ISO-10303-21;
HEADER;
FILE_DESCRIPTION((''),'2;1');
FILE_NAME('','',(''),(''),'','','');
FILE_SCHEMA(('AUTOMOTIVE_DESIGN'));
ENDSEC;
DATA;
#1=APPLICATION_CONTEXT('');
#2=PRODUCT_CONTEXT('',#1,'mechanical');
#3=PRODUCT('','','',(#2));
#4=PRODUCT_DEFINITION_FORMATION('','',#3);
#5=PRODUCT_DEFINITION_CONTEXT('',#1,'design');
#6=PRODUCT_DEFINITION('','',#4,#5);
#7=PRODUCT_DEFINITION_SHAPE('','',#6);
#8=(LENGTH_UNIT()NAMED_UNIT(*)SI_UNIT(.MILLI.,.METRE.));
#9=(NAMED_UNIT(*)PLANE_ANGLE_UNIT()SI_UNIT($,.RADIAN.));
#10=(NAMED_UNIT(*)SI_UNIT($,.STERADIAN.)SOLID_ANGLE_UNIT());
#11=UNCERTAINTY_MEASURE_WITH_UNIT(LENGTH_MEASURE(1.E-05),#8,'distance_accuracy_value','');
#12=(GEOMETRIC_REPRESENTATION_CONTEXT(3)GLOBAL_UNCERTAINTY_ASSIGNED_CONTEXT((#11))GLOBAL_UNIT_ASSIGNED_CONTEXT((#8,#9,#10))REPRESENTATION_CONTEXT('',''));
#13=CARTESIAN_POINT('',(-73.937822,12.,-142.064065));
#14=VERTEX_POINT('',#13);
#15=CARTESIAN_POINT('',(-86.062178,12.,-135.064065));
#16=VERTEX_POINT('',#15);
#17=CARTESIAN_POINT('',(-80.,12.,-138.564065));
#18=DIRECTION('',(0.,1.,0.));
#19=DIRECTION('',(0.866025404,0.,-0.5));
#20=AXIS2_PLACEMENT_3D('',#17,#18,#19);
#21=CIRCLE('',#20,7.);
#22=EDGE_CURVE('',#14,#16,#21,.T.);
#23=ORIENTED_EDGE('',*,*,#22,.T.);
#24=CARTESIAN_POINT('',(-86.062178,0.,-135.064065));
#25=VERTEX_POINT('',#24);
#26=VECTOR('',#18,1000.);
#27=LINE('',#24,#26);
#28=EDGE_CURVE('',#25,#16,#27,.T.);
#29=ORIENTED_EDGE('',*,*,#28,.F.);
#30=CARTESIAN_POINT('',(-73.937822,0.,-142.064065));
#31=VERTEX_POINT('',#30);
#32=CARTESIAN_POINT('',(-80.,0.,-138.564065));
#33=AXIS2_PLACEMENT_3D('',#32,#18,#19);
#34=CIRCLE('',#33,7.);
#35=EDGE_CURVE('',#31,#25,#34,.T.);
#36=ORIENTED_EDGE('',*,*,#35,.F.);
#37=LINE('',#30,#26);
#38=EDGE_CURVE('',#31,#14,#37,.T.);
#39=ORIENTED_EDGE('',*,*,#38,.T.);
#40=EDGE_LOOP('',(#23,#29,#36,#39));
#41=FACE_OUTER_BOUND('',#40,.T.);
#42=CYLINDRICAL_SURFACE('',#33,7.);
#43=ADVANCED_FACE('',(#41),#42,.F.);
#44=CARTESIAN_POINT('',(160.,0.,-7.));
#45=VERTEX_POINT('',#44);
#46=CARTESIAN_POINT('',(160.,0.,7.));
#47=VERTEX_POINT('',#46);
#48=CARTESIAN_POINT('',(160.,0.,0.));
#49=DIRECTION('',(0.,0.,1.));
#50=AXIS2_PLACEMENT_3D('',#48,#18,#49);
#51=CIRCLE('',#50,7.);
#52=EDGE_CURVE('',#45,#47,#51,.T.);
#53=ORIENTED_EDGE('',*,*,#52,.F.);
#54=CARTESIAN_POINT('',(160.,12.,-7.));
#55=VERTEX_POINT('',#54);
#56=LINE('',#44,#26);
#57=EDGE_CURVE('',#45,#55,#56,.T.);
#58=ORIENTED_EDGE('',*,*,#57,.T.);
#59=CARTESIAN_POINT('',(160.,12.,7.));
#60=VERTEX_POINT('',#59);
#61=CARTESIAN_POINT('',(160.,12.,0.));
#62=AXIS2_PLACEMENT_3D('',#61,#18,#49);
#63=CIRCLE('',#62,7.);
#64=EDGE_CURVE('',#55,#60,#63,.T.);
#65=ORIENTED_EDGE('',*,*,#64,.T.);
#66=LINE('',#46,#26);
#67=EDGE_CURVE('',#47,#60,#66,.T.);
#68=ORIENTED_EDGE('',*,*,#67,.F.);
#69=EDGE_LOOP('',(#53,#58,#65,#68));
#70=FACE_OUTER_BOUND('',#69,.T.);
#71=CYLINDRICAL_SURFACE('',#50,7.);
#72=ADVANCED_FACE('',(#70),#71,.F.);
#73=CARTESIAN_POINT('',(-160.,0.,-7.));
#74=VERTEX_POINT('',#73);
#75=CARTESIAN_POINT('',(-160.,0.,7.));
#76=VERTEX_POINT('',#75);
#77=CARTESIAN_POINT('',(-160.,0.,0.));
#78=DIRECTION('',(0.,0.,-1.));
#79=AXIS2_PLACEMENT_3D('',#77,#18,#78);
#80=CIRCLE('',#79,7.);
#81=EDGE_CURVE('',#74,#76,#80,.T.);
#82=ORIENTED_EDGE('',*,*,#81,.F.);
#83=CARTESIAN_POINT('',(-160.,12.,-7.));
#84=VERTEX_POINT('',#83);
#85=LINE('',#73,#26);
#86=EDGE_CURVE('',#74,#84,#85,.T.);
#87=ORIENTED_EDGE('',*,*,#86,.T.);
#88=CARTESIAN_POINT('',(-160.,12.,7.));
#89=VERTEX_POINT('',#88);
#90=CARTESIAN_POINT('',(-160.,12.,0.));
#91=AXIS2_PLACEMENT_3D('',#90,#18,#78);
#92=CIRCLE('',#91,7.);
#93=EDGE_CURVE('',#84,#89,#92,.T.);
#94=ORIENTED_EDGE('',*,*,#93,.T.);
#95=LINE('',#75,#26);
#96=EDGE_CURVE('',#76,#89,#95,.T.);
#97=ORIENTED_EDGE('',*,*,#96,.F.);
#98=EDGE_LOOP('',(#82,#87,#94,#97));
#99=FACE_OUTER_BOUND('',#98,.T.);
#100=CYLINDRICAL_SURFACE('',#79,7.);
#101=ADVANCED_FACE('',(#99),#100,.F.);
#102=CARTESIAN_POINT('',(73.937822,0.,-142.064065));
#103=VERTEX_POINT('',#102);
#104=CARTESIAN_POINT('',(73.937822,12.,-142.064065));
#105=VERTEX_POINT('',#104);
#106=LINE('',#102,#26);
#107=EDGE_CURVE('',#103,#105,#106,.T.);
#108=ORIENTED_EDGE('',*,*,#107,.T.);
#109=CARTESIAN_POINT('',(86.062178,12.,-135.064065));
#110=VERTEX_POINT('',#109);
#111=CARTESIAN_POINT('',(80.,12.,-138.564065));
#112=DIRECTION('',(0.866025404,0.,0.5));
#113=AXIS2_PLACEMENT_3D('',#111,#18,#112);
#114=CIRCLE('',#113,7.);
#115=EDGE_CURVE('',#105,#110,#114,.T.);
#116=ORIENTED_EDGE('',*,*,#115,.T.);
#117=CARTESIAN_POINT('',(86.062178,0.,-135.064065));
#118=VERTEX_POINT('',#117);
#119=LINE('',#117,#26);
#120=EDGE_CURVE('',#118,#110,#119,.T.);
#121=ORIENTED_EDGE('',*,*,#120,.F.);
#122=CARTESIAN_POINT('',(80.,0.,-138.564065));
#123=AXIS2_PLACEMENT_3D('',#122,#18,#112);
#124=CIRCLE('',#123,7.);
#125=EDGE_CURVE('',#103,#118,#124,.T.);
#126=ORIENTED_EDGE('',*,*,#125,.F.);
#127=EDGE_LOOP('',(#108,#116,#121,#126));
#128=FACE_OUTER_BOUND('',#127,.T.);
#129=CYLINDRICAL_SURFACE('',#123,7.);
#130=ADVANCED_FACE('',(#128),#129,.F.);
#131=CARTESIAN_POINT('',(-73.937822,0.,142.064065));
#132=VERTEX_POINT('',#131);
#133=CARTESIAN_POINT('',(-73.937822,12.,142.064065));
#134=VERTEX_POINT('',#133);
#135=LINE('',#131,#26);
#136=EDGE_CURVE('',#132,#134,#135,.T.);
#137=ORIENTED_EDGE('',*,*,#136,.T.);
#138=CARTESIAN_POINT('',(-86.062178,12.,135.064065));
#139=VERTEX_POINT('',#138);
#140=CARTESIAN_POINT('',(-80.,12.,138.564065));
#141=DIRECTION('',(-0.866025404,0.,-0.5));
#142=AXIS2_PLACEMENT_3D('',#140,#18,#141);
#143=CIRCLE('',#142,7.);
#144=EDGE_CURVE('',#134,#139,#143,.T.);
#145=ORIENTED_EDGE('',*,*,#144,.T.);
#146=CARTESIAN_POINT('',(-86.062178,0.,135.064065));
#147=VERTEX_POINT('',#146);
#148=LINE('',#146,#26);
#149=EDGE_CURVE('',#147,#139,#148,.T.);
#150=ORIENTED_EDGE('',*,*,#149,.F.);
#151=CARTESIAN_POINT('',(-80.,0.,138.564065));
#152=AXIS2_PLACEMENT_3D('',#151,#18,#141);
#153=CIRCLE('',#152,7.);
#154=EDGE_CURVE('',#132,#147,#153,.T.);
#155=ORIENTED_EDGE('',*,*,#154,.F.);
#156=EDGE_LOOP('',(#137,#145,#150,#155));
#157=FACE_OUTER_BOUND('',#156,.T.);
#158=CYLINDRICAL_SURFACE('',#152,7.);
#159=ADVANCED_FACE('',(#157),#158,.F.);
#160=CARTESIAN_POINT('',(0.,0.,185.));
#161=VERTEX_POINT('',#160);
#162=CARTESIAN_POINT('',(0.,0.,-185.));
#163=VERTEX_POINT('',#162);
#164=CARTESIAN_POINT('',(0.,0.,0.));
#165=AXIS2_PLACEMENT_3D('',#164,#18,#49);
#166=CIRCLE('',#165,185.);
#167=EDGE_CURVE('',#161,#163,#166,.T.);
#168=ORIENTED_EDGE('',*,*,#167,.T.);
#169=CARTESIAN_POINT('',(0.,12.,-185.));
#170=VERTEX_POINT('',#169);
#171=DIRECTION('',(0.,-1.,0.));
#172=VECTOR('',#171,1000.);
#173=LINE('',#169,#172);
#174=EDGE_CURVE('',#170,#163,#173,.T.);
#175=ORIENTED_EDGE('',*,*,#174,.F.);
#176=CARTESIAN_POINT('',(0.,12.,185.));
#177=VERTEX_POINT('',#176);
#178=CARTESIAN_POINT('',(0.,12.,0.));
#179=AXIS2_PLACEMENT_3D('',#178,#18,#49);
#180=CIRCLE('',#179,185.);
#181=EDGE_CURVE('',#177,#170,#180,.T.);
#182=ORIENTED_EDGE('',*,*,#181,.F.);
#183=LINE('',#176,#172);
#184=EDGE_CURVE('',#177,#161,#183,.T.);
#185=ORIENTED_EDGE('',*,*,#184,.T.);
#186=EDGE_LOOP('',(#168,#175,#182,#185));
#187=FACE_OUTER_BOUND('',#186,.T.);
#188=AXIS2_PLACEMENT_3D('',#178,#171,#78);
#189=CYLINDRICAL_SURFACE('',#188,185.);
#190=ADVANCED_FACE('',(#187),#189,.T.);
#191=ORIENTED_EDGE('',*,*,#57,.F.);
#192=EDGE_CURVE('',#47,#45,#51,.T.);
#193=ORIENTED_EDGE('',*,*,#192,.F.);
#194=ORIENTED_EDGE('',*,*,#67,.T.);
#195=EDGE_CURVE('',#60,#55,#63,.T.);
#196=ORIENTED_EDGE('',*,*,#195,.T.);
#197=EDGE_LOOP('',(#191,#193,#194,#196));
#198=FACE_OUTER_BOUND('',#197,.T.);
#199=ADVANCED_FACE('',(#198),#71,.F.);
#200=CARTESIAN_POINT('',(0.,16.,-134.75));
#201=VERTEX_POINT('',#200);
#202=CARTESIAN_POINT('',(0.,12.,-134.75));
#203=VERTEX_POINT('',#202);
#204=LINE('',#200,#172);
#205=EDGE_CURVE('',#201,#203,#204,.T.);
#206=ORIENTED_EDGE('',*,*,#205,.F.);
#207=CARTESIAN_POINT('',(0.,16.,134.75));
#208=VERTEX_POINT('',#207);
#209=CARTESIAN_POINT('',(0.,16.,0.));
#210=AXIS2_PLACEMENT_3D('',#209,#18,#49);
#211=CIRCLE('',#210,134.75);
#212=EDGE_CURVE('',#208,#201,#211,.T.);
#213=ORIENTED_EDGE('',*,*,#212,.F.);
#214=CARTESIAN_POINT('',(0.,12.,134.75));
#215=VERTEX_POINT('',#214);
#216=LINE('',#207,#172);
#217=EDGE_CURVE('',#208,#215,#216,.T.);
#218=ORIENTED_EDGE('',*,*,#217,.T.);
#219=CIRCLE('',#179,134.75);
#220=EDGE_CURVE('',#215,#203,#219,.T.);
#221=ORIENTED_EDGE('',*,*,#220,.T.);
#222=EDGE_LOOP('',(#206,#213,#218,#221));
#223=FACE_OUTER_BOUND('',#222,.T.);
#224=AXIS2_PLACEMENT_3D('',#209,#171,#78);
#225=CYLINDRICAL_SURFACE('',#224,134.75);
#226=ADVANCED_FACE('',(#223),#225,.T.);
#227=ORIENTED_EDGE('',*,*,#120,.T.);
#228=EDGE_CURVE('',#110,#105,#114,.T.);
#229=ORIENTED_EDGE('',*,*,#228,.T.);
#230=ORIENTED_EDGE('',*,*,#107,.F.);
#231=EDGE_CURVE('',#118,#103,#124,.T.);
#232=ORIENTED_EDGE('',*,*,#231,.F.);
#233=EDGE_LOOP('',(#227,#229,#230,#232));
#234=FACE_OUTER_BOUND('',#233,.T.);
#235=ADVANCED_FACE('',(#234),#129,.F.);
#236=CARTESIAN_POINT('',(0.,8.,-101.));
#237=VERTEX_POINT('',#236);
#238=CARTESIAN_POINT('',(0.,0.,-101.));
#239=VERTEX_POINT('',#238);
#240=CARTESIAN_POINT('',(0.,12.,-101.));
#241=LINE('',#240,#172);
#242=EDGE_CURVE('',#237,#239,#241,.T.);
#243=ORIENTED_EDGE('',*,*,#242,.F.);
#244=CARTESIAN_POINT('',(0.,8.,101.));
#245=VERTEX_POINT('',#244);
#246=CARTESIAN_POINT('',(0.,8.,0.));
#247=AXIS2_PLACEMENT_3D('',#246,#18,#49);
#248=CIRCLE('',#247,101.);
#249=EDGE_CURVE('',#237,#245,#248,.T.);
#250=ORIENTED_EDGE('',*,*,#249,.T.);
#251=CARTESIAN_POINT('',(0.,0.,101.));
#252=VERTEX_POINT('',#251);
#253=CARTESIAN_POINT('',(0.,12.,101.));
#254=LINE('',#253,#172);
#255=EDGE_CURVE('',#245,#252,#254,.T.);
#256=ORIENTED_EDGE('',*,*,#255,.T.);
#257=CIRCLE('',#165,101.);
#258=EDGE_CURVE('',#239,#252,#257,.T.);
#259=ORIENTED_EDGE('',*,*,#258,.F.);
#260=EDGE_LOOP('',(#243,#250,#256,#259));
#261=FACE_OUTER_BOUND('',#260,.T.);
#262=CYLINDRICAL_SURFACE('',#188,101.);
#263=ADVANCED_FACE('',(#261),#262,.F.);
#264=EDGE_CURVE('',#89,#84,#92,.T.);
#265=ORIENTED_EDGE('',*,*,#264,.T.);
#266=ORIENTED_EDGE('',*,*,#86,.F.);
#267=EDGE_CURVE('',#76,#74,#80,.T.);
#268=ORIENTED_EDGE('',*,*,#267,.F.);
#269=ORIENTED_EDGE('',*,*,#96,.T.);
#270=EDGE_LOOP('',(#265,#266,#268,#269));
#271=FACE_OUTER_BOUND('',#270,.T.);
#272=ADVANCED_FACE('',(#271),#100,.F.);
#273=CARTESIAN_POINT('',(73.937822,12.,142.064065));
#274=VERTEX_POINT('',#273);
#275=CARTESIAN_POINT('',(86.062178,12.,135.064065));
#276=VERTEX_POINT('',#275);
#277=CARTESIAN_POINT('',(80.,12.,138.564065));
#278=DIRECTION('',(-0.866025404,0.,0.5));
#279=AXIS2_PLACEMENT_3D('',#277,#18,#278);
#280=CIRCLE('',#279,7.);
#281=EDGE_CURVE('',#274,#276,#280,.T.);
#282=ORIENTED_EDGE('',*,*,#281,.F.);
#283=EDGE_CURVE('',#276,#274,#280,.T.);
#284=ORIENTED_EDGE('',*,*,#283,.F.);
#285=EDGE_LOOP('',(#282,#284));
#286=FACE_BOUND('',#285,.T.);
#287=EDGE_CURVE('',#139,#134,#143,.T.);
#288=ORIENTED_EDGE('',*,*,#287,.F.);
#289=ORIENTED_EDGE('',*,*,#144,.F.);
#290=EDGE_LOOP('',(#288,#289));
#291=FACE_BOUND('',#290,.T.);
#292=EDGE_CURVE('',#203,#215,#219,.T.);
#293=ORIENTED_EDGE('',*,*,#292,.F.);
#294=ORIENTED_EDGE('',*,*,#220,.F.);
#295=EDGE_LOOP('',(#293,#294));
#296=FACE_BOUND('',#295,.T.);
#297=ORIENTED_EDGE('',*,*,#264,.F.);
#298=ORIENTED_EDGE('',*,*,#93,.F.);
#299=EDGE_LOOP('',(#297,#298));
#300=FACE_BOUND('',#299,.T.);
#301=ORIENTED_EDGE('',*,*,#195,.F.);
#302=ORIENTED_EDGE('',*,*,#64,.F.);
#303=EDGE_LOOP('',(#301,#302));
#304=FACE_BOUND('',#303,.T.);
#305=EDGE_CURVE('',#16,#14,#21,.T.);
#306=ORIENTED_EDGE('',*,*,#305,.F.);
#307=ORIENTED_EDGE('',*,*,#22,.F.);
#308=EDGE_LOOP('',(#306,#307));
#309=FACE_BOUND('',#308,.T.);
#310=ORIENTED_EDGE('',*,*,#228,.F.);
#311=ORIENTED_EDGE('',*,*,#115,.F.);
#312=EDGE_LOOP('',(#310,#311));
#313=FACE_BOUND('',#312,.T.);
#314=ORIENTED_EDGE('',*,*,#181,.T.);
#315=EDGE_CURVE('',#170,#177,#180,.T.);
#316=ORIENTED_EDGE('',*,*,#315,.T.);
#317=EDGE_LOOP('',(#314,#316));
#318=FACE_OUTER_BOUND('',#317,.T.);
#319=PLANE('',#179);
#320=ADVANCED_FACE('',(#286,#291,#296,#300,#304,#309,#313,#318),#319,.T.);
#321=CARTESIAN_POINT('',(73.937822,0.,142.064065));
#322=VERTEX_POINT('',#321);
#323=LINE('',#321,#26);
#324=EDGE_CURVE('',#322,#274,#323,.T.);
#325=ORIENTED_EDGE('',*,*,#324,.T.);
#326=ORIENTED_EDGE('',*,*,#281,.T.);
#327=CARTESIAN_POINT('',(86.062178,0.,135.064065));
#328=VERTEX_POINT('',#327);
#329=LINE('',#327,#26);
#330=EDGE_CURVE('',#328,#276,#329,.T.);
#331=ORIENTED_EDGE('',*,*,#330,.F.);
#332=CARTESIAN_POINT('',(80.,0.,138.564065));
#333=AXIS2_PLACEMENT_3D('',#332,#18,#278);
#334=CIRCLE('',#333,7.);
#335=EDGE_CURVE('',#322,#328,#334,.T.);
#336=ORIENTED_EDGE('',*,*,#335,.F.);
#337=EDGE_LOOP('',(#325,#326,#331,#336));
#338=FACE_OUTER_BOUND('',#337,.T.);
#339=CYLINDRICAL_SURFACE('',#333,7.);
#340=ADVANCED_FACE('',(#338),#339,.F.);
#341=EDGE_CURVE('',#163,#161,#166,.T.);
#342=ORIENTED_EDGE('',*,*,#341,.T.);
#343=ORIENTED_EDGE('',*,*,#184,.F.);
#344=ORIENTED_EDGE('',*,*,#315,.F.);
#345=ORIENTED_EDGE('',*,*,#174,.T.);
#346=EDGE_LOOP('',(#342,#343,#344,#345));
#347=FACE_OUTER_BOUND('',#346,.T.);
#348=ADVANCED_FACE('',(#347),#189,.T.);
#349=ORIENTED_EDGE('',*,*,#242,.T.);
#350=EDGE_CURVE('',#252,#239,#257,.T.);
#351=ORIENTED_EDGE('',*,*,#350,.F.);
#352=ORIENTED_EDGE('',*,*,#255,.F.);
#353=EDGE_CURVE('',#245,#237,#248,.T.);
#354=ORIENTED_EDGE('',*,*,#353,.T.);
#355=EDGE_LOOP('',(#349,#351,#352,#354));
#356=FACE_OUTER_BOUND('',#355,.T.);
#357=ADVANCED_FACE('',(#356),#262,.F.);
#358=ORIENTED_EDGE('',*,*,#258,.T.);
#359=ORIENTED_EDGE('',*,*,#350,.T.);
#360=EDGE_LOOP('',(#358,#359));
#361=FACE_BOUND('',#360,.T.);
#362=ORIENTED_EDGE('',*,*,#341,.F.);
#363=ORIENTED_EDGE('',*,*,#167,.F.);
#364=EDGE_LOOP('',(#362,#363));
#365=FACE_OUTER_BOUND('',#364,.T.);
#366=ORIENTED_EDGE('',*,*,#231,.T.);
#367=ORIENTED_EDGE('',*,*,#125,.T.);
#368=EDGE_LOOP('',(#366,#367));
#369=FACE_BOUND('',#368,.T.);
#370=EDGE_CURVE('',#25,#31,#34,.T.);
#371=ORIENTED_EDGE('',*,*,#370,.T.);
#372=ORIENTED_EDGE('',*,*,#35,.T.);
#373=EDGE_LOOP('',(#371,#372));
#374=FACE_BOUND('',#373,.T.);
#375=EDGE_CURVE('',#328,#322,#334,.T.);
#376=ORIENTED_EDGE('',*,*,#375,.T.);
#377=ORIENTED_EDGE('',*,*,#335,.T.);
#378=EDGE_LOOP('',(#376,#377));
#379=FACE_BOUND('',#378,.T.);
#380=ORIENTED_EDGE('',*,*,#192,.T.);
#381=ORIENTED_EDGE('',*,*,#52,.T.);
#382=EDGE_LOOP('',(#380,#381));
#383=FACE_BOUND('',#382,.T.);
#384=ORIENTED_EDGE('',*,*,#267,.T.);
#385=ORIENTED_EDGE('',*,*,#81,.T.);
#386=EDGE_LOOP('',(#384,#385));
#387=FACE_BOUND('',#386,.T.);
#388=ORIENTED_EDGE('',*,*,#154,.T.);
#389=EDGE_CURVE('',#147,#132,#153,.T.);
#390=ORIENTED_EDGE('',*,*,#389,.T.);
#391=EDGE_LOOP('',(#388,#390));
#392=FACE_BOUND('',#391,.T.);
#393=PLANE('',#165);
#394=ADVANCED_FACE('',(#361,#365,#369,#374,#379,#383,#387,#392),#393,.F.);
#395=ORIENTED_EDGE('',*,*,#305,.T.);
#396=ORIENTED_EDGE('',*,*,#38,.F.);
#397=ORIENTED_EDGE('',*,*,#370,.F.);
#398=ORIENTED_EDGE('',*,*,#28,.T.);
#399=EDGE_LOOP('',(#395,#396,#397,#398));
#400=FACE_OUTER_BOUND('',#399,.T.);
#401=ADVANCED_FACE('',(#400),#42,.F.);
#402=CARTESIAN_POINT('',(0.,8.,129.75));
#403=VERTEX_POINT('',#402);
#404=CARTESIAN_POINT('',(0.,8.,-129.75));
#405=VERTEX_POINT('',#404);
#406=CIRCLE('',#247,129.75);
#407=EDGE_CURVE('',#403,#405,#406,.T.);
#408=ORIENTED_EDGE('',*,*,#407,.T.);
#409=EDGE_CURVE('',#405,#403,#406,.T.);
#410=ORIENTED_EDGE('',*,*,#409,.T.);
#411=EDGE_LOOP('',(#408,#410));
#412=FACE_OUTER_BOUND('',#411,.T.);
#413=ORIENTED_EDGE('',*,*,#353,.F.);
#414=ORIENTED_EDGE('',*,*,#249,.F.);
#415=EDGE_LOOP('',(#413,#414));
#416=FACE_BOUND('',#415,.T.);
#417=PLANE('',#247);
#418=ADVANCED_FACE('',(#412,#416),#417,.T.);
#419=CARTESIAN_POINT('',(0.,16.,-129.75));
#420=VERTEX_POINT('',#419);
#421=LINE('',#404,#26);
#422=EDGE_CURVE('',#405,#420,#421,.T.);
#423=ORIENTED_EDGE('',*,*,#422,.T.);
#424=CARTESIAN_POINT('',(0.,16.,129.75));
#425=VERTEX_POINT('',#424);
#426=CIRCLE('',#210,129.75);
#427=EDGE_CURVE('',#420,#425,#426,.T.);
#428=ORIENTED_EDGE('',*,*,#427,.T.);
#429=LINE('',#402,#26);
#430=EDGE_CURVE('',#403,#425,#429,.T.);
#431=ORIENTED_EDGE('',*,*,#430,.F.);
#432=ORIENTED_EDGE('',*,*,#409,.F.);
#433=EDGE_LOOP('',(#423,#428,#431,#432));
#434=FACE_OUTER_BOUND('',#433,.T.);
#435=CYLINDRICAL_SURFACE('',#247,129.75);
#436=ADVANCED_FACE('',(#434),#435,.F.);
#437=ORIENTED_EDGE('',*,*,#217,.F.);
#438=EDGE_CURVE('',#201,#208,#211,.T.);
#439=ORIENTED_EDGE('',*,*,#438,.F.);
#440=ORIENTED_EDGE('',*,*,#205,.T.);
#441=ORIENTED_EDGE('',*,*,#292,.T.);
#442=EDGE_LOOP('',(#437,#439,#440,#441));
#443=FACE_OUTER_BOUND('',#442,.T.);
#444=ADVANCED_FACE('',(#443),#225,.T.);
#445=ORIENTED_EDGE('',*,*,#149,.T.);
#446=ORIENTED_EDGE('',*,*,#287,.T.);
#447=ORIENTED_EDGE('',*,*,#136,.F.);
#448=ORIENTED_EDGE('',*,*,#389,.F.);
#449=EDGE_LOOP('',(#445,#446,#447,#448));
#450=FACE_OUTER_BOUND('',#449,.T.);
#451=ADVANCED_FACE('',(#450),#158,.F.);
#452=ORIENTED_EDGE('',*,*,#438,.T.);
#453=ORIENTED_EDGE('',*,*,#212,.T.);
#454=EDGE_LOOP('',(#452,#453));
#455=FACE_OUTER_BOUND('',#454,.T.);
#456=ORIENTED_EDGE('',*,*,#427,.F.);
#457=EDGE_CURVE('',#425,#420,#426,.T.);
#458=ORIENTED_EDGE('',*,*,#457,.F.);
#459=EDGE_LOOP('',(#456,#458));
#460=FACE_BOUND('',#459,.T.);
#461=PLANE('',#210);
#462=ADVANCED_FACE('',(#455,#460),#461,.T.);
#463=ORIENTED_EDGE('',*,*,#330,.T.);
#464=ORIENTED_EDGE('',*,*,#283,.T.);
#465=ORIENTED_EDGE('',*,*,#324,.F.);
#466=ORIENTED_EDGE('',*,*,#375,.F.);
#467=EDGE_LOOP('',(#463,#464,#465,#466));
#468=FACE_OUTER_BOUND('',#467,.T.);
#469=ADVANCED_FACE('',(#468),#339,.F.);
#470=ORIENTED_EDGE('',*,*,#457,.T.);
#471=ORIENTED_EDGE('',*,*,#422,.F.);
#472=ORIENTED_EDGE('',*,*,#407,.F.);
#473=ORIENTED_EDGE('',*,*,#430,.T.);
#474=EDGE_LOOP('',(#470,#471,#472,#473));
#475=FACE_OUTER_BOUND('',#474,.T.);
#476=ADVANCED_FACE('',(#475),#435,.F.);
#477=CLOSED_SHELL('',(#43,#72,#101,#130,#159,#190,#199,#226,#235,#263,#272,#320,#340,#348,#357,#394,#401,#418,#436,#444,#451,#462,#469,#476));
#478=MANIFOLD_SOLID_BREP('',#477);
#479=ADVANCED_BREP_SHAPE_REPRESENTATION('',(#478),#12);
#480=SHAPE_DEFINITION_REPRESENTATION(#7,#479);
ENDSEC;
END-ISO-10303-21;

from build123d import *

# Parameters (mm, degrees)
SKETCH1_R           = 185
SKETCH1_R_2         = 101
BOSS_EXTRUDE1_DEPTH = 12
SKETCH2_R           = 129.75
CUT_EXTRUDE1_DEPTH  = 4
BOSS_EXTRUDE2_START = 4
SKETCH3_R           = 134.75
SKETCH3_R_2         = 129.75
BOSS_EXTRUDE2_DEPTH = 4
SKETCH4_R           = 7
CUT_EXTRUDE2_DEPTH  = 262.90456277
CIRPATTERN1_COUNT   = 6


with BuildPart() as part:
    # Sketch1 → Boss-Extrude1 (new body)
    with BuildSketch(Plane(origin=(0, 0, 0), x_dir=(1, 0, 0), z_dir=(0, 1, 0))):
        with Locations(Location((0, 0, 0), (0, 0, 270))):
            Circle(SKETCH1_R)
        with Locations(Location((0, 0, 0), (0, 0, 270))):
            Circle(SKETCH1_R_2, mode=Mode.SUBTRACT)
    extrude(amount=BOSS_EXTRUDE1_DEPTH)

    # Sketch2 → Cut-Extrude1 (cut)
    with BuildSketch(Plane(origin=(0, 12, 0), x_dir=(1, 0, 0), z_dir=(0, 1, 0))):
        with Locations(Location((0, 0, 0), (0, 0, 270))):
            Circle(SKETCH2_R)
    extrude(amount=-CUT_EXTRUDE1_DEPTH, mode=Mode.SUBTRACT)

    # Sketch3 → Boss-Extrude2 (add)
    with BuildSketch(Plane(origin=(0, 12, 0), x_dir=(1, 0, 0), z_dir=(0, 1, 0)).offset(BOSS_EXTRUDE2_START)):
        with Locations(Location((0, 0, 0), (0, 0, 270))):
            Circle(SKETCH3_R)
        with Locations(Location((0, 0, 0), (0, 0, 270))):
            Circle(SKETCH3_R_2, mode=Mode.SUBTRACT)
    extrude(amount=-BOSS_EXTRUDE2_DEPTH)

    # Sketch4 → Cut-Extrude2 (cut, through all)
    with BuildSketch(Plane(origin=(0, 12, 0), x_dir=(1, 0, 0), z_dir=(0, 1, 0))):
        with Locations(Location((160, 0, 0), (0, 0, 270))):
            Circle(SKETCH4_R)
    cut_extrude2 = extrude(amount=-CUT_EXTRUDE2_DEPTH, mode=Mode.SUBTRACT)

    # CirPattern1: Cut-Extrude2 ×6 about axis
    cirpattern1_axis = Axis((0, 0, 0), (0, 1, 0))
    for i in range(1, CIRPATTERN1_COUNT):
        add(cut_extrude2.rotate(cirpattern1_axis, i * 360 / CIRPATTERN1_COUNT), mode=Mode.SUBTRACT)


solid = part.part
